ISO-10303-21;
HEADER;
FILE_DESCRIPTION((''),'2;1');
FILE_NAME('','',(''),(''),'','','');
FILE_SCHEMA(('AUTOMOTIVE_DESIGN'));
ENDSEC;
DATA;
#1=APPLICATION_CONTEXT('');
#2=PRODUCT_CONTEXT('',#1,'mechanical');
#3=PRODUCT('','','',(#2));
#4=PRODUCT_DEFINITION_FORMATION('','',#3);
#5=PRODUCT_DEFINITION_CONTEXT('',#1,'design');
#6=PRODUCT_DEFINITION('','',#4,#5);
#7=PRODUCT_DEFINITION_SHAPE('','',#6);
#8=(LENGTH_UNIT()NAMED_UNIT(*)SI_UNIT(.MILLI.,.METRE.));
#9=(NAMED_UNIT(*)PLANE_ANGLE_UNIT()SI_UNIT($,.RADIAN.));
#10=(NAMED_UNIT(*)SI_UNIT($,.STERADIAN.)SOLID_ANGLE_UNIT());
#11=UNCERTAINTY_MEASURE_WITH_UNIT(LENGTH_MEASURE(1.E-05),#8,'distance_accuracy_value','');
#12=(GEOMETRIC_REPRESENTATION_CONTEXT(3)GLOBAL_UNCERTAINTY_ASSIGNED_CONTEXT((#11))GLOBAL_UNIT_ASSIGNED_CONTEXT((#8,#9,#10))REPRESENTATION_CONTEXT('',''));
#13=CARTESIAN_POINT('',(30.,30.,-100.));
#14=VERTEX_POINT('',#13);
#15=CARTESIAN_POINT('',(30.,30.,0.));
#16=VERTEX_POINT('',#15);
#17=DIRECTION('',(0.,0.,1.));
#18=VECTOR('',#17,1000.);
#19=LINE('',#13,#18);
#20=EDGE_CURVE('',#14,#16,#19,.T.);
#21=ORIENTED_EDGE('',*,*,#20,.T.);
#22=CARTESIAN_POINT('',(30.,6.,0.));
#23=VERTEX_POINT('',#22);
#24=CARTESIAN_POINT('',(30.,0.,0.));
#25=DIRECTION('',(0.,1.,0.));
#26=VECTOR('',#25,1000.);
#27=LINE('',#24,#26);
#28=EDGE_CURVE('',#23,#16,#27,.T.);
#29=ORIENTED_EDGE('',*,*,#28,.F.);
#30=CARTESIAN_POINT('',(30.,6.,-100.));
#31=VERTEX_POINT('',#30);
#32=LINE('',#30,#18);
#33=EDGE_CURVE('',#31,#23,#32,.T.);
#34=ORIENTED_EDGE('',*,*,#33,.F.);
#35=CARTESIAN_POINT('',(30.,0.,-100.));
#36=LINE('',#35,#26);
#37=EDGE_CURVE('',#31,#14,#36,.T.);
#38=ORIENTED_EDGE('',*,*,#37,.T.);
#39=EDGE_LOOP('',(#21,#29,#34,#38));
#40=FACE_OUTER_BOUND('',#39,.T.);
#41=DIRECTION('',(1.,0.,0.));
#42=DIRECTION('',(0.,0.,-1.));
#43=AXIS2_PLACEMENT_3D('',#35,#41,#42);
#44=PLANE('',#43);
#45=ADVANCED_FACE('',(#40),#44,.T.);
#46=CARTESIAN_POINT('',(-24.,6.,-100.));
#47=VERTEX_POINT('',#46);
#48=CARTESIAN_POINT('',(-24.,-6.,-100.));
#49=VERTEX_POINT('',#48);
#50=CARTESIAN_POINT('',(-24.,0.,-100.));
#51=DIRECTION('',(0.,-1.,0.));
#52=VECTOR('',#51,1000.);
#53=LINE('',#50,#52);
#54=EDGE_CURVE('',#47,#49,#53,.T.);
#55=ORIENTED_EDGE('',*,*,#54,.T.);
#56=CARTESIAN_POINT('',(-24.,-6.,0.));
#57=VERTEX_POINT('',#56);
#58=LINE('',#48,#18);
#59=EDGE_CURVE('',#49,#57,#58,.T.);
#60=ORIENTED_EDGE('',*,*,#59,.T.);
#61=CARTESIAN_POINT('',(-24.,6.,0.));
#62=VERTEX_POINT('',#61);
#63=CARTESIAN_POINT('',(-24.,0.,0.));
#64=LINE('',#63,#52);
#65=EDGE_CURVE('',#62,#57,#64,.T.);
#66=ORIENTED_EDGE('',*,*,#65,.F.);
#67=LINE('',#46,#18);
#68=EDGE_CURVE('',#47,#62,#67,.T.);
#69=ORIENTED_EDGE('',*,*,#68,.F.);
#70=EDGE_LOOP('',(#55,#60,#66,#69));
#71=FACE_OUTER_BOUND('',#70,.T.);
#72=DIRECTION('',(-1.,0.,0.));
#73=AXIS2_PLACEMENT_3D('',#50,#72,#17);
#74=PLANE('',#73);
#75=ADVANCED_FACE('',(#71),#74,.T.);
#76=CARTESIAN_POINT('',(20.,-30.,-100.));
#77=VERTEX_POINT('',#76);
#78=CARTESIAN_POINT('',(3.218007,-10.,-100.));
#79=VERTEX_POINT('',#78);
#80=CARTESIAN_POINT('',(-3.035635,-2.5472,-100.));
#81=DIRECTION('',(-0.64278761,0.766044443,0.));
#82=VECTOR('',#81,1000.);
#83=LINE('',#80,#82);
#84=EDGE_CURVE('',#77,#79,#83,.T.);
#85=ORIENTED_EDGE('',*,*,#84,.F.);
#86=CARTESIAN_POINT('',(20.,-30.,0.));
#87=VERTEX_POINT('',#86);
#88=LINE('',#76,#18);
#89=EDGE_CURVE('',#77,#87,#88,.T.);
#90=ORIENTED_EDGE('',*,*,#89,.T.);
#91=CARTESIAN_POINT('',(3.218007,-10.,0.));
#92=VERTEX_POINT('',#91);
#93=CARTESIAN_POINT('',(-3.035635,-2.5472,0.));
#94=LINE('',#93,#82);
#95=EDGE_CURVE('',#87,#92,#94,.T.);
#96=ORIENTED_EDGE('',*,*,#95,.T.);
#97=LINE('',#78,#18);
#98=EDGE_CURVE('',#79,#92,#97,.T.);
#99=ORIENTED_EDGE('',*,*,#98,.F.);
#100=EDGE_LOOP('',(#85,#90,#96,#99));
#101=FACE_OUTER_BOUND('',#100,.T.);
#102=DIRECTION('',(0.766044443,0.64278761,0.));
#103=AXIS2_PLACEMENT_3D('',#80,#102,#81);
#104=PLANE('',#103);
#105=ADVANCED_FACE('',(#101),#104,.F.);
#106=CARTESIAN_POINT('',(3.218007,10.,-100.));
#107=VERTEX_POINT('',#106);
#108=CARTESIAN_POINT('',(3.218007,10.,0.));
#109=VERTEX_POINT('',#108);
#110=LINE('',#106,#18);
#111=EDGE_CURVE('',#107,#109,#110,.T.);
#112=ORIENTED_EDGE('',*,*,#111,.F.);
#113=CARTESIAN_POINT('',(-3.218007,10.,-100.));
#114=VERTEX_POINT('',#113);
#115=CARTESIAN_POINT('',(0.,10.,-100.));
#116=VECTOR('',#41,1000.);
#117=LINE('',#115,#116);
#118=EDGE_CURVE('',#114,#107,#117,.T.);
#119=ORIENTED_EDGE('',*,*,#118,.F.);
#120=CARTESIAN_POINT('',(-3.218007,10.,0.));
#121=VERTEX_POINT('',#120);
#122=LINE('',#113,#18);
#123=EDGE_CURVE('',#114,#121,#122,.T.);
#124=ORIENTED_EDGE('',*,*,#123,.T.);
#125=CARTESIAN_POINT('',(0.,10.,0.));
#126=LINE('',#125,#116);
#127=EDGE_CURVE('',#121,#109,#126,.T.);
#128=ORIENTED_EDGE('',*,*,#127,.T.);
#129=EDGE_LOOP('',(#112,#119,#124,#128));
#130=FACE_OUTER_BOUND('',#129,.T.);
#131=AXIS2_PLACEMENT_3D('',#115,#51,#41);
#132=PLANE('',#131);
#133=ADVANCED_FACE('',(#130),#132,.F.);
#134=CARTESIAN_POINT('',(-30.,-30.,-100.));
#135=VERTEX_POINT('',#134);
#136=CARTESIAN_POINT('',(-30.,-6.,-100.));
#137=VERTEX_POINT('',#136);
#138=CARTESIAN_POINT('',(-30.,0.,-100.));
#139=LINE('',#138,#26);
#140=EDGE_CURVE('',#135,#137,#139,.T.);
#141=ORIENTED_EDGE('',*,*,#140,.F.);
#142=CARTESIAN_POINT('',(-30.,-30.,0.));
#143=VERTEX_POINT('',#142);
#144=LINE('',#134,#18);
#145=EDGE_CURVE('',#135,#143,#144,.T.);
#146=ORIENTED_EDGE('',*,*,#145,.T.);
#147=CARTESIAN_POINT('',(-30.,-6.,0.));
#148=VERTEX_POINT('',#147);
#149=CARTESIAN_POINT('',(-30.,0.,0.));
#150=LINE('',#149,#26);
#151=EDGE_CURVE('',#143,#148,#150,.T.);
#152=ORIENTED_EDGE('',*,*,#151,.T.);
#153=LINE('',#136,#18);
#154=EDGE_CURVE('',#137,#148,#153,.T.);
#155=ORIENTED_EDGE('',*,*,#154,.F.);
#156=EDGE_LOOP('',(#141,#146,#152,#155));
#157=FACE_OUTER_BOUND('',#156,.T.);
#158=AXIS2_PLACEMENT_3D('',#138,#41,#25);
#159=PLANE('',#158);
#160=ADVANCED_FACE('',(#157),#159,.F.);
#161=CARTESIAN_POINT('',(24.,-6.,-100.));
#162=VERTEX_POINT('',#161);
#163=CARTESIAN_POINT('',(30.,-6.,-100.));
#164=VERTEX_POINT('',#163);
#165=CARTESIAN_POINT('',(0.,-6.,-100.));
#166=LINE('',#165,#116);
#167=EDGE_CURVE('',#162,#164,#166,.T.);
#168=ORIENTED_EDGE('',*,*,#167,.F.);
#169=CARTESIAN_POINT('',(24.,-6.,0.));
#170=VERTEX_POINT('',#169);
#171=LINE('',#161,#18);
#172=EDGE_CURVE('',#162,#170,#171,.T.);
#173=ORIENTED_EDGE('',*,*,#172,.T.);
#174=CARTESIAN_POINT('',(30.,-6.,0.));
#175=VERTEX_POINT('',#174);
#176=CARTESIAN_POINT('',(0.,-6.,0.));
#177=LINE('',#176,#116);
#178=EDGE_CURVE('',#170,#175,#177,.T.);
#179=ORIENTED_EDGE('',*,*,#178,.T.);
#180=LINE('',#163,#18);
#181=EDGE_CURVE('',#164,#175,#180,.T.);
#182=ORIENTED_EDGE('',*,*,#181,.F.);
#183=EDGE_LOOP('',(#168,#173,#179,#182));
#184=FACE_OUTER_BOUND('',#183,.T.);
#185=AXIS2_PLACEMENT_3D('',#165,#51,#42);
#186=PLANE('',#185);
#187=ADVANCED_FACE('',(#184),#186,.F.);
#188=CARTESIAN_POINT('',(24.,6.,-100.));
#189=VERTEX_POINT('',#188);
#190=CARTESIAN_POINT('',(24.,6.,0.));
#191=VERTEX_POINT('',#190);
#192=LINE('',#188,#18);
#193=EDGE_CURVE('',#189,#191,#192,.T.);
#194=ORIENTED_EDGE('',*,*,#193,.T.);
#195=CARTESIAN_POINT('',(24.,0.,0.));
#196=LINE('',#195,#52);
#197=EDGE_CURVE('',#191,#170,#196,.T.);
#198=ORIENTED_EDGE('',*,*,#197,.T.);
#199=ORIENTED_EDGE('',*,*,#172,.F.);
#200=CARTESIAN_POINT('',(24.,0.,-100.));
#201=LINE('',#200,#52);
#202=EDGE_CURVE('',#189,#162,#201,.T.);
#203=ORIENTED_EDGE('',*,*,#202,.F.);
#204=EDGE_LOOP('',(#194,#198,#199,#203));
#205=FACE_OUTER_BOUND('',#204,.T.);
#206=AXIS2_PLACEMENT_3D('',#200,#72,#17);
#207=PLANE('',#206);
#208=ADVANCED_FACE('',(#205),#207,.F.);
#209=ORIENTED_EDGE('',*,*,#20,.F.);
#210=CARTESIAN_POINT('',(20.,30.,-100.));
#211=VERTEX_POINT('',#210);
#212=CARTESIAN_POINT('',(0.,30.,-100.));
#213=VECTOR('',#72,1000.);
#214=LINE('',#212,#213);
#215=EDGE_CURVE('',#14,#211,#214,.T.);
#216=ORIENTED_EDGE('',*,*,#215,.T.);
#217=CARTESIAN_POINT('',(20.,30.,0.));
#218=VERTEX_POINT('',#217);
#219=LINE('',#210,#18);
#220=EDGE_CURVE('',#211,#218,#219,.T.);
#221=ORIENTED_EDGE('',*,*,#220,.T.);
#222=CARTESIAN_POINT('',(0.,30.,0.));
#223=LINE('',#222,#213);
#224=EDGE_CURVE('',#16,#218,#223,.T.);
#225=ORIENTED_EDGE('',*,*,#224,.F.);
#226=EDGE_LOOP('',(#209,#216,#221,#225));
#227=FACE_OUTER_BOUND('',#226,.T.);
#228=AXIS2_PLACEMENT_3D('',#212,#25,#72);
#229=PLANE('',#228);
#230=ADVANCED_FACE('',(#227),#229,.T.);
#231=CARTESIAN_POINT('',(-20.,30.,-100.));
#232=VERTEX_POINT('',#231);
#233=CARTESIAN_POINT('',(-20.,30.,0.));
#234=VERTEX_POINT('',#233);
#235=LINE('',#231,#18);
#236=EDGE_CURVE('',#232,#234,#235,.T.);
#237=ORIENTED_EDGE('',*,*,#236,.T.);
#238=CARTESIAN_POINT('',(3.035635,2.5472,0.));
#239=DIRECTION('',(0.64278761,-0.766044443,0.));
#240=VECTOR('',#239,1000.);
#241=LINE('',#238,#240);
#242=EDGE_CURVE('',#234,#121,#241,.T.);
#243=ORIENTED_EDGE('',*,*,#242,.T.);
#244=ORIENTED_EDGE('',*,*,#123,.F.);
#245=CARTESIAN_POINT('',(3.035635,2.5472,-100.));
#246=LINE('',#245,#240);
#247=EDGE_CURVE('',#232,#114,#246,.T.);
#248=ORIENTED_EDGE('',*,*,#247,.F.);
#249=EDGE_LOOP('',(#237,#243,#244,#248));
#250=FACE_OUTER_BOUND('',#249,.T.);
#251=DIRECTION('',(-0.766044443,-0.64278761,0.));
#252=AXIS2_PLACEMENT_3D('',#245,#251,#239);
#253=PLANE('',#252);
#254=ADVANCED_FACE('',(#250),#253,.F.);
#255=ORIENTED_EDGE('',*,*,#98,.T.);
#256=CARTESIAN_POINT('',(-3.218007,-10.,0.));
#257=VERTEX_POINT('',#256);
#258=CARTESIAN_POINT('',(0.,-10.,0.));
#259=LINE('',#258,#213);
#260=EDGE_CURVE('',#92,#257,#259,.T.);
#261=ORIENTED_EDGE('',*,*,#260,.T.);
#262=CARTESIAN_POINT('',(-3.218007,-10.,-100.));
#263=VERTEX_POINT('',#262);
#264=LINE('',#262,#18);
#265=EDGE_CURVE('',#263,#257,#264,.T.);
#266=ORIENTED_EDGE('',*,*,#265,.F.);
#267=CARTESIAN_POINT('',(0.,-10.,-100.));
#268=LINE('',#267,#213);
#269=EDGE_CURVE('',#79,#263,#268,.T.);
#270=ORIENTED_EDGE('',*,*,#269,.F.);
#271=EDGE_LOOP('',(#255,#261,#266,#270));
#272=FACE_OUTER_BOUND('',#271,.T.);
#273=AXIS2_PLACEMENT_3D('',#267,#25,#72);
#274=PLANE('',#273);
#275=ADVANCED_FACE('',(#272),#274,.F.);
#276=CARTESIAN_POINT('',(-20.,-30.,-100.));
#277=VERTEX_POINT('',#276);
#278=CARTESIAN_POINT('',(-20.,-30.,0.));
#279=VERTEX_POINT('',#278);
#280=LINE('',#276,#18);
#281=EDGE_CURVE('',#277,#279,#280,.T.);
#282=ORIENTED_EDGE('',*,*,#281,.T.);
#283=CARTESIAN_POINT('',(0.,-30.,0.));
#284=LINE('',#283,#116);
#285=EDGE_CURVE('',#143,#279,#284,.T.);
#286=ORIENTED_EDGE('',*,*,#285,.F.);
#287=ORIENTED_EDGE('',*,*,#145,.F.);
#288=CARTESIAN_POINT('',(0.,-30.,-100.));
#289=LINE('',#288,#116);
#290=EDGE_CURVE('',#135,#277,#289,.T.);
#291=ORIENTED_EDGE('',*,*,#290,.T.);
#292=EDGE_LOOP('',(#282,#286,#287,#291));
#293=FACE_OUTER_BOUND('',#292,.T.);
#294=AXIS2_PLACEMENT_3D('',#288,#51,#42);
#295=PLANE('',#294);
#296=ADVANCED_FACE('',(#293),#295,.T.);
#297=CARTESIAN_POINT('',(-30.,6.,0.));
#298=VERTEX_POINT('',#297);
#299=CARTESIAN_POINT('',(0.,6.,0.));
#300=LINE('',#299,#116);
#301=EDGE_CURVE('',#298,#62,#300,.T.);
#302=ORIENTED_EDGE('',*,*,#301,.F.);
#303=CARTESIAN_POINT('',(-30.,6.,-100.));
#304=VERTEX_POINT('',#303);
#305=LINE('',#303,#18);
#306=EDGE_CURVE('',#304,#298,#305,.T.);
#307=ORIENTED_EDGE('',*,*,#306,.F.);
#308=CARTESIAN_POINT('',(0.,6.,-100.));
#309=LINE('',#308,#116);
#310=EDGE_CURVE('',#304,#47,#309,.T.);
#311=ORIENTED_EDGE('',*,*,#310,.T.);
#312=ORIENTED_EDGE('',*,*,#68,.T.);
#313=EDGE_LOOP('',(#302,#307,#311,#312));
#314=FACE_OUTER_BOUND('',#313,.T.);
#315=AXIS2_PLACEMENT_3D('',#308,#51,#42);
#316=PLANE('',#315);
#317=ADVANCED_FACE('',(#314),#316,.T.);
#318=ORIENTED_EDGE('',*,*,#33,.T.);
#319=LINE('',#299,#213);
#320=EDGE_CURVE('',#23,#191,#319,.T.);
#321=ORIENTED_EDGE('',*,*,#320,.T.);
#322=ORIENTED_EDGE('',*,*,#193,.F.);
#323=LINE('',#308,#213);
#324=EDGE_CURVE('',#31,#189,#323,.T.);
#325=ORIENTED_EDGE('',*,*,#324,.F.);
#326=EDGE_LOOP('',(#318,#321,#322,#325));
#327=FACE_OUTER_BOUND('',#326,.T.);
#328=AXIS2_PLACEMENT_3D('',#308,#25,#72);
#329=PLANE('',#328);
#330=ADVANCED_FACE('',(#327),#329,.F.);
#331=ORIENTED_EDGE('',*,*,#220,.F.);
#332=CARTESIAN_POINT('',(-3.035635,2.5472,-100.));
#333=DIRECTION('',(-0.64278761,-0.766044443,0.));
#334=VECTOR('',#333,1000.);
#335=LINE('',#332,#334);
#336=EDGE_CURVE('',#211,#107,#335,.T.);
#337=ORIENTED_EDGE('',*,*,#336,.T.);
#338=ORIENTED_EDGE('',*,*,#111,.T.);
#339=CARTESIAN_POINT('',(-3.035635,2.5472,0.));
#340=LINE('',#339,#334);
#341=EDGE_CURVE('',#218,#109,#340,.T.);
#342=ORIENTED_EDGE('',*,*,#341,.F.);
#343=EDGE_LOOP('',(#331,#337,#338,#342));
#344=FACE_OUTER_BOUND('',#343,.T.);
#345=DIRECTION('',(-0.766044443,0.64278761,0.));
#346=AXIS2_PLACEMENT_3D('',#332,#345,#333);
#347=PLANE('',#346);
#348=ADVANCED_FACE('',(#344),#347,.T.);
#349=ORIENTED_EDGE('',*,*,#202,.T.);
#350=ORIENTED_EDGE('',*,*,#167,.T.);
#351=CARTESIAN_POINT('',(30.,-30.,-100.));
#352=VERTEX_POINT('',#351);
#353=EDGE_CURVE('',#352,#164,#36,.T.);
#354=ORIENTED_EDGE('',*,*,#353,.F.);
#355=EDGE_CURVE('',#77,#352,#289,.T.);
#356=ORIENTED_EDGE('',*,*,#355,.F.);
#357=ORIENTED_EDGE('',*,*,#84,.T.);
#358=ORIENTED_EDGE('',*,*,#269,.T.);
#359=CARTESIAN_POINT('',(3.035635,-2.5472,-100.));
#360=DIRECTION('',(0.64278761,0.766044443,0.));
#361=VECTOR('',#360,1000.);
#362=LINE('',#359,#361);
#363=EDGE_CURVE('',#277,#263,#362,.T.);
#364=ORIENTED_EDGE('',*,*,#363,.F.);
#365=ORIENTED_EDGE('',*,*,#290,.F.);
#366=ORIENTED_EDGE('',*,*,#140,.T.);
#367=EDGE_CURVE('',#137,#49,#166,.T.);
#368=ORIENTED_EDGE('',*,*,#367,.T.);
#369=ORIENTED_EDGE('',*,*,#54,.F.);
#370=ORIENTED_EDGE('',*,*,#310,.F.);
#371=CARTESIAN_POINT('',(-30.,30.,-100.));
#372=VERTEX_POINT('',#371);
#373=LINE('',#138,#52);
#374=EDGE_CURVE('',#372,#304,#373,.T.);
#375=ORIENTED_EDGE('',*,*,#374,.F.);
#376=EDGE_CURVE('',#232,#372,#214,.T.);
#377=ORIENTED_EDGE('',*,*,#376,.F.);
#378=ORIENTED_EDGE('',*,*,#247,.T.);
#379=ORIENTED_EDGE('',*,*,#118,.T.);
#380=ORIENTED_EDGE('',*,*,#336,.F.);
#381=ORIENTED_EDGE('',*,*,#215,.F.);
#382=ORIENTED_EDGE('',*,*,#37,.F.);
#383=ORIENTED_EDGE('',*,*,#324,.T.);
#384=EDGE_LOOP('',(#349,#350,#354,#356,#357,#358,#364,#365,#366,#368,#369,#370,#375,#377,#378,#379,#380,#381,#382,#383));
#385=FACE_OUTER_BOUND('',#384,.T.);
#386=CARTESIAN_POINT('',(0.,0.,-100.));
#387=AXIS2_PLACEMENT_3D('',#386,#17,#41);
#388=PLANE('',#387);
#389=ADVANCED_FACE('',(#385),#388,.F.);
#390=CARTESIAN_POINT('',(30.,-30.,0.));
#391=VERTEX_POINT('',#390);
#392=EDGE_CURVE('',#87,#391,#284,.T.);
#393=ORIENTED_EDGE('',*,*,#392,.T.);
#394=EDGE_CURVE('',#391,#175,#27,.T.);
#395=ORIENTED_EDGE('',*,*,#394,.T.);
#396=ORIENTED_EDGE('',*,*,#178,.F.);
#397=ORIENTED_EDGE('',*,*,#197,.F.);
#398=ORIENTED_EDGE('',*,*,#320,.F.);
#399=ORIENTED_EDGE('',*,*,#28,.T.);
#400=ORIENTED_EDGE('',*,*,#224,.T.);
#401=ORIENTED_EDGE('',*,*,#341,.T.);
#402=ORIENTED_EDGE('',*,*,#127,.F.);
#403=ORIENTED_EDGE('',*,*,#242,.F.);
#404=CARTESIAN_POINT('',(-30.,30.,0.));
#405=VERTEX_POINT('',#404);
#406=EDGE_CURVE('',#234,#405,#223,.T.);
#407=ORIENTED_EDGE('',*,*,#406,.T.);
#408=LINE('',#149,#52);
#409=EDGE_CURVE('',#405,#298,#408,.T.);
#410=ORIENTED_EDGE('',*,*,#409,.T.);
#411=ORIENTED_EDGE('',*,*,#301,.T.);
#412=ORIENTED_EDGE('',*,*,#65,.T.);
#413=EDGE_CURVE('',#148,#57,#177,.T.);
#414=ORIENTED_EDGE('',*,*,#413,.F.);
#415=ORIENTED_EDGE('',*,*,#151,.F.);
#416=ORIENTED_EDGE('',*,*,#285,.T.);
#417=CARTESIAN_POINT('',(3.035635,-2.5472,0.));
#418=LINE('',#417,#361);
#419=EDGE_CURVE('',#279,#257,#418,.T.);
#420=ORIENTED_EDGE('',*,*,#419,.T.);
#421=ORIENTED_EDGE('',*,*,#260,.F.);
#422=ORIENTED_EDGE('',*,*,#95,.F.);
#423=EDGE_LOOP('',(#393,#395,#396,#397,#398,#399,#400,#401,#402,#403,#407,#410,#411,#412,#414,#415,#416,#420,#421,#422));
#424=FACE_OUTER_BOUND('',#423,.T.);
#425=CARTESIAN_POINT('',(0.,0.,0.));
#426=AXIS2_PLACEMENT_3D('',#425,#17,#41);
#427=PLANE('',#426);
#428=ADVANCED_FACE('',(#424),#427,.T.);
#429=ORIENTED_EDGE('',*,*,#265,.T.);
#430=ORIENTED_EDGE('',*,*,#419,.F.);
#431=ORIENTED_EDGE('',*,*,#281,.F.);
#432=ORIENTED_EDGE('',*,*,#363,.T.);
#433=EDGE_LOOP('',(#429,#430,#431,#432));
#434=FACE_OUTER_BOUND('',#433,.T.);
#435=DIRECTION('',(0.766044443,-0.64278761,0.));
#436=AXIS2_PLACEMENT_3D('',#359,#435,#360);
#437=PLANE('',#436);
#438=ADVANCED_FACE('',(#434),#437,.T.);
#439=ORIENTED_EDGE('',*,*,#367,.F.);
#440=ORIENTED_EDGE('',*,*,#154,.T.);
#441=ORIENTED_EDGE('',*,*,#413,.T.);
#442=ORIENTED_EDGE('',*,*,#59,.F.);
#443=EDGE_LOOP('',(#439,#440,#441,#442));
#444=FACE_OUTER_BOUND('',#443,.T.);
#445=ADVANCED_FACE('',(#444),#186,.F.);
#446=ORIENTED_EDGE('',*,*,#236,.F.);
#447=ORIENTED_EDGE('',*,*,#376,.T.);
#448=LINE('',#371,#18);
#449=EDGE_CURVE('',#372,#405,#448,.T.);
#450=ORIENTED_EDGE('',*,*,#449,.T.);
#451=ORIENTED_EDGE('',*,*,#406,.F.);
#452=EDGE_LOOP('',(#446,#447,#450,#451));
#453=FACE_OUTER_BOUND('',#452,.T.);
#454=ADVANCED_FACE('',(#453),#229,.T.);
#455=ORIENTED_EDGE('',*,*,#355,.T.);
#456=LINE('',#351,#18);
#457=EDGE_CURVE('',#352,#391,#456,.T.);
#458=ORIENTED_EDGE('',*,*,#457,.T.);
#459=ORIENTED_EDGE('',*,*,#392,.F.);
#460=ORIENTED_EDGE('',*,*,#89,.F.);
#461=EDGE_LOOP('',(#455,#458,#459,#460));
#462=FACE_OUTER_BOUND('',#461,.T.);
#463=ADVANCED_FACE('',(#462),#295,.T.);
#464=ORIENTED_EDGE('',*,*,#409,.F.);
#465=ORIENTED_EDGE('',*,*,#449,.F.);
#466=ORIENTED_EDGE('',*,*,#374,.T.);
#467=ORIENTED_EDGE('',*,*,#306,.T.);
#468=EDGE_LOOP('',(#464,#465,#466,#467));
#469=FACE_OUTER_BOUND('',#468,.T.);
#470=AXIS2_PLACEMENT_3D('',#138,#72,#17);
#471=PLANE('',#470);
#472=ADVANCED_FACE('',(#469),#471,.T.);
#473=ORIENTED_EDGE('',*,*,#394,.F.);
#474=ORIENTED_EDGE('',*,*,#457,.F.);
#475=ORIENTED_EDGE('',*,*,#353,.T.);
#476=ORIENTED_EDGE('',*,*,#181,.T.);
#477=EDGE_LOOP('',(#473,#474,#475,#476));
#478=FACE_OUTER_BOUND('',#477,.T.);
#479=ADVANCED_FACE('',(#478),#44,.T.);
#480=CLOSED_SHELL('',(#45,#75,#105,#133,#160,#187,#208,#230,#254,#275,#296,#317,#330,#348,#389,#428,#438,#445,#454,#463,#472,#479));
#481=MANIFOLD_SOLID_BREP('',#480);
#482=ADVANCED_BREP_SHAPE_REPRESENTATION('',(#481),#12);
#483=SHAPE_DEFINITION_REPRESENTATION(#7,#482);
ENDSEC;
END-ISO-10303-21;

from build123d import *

# Parameters (mm, degrees)
V_BLOCK_BODY_EXTRUDE_100_DEPTH = 100


with BuildPart() as part:
    # V-Block Profile Sketch → V-Block Body Extrude 100 (new body)
    with BuildSketch(Plane.XY):
        Polygon((-30, -6), (-30, -30), (-20, -30), (-3.218007376, -10), (0, -10), (3.218007376, -10), (20, -30), (30, -30), (30, -6), (24, -6), (24, 6), (30, 6), (30, 30), (20, 30), (3.218007376, 10), (0, 10), (-3.218007376, 10), (-20, 30), (-30, 30), (-30, 6), (-24, 6), (-24, -6), align=None)
    extrude(amount=-V_BLOCK_BODY_EXTRUDE_100_DEPTH)


solid = part.part
